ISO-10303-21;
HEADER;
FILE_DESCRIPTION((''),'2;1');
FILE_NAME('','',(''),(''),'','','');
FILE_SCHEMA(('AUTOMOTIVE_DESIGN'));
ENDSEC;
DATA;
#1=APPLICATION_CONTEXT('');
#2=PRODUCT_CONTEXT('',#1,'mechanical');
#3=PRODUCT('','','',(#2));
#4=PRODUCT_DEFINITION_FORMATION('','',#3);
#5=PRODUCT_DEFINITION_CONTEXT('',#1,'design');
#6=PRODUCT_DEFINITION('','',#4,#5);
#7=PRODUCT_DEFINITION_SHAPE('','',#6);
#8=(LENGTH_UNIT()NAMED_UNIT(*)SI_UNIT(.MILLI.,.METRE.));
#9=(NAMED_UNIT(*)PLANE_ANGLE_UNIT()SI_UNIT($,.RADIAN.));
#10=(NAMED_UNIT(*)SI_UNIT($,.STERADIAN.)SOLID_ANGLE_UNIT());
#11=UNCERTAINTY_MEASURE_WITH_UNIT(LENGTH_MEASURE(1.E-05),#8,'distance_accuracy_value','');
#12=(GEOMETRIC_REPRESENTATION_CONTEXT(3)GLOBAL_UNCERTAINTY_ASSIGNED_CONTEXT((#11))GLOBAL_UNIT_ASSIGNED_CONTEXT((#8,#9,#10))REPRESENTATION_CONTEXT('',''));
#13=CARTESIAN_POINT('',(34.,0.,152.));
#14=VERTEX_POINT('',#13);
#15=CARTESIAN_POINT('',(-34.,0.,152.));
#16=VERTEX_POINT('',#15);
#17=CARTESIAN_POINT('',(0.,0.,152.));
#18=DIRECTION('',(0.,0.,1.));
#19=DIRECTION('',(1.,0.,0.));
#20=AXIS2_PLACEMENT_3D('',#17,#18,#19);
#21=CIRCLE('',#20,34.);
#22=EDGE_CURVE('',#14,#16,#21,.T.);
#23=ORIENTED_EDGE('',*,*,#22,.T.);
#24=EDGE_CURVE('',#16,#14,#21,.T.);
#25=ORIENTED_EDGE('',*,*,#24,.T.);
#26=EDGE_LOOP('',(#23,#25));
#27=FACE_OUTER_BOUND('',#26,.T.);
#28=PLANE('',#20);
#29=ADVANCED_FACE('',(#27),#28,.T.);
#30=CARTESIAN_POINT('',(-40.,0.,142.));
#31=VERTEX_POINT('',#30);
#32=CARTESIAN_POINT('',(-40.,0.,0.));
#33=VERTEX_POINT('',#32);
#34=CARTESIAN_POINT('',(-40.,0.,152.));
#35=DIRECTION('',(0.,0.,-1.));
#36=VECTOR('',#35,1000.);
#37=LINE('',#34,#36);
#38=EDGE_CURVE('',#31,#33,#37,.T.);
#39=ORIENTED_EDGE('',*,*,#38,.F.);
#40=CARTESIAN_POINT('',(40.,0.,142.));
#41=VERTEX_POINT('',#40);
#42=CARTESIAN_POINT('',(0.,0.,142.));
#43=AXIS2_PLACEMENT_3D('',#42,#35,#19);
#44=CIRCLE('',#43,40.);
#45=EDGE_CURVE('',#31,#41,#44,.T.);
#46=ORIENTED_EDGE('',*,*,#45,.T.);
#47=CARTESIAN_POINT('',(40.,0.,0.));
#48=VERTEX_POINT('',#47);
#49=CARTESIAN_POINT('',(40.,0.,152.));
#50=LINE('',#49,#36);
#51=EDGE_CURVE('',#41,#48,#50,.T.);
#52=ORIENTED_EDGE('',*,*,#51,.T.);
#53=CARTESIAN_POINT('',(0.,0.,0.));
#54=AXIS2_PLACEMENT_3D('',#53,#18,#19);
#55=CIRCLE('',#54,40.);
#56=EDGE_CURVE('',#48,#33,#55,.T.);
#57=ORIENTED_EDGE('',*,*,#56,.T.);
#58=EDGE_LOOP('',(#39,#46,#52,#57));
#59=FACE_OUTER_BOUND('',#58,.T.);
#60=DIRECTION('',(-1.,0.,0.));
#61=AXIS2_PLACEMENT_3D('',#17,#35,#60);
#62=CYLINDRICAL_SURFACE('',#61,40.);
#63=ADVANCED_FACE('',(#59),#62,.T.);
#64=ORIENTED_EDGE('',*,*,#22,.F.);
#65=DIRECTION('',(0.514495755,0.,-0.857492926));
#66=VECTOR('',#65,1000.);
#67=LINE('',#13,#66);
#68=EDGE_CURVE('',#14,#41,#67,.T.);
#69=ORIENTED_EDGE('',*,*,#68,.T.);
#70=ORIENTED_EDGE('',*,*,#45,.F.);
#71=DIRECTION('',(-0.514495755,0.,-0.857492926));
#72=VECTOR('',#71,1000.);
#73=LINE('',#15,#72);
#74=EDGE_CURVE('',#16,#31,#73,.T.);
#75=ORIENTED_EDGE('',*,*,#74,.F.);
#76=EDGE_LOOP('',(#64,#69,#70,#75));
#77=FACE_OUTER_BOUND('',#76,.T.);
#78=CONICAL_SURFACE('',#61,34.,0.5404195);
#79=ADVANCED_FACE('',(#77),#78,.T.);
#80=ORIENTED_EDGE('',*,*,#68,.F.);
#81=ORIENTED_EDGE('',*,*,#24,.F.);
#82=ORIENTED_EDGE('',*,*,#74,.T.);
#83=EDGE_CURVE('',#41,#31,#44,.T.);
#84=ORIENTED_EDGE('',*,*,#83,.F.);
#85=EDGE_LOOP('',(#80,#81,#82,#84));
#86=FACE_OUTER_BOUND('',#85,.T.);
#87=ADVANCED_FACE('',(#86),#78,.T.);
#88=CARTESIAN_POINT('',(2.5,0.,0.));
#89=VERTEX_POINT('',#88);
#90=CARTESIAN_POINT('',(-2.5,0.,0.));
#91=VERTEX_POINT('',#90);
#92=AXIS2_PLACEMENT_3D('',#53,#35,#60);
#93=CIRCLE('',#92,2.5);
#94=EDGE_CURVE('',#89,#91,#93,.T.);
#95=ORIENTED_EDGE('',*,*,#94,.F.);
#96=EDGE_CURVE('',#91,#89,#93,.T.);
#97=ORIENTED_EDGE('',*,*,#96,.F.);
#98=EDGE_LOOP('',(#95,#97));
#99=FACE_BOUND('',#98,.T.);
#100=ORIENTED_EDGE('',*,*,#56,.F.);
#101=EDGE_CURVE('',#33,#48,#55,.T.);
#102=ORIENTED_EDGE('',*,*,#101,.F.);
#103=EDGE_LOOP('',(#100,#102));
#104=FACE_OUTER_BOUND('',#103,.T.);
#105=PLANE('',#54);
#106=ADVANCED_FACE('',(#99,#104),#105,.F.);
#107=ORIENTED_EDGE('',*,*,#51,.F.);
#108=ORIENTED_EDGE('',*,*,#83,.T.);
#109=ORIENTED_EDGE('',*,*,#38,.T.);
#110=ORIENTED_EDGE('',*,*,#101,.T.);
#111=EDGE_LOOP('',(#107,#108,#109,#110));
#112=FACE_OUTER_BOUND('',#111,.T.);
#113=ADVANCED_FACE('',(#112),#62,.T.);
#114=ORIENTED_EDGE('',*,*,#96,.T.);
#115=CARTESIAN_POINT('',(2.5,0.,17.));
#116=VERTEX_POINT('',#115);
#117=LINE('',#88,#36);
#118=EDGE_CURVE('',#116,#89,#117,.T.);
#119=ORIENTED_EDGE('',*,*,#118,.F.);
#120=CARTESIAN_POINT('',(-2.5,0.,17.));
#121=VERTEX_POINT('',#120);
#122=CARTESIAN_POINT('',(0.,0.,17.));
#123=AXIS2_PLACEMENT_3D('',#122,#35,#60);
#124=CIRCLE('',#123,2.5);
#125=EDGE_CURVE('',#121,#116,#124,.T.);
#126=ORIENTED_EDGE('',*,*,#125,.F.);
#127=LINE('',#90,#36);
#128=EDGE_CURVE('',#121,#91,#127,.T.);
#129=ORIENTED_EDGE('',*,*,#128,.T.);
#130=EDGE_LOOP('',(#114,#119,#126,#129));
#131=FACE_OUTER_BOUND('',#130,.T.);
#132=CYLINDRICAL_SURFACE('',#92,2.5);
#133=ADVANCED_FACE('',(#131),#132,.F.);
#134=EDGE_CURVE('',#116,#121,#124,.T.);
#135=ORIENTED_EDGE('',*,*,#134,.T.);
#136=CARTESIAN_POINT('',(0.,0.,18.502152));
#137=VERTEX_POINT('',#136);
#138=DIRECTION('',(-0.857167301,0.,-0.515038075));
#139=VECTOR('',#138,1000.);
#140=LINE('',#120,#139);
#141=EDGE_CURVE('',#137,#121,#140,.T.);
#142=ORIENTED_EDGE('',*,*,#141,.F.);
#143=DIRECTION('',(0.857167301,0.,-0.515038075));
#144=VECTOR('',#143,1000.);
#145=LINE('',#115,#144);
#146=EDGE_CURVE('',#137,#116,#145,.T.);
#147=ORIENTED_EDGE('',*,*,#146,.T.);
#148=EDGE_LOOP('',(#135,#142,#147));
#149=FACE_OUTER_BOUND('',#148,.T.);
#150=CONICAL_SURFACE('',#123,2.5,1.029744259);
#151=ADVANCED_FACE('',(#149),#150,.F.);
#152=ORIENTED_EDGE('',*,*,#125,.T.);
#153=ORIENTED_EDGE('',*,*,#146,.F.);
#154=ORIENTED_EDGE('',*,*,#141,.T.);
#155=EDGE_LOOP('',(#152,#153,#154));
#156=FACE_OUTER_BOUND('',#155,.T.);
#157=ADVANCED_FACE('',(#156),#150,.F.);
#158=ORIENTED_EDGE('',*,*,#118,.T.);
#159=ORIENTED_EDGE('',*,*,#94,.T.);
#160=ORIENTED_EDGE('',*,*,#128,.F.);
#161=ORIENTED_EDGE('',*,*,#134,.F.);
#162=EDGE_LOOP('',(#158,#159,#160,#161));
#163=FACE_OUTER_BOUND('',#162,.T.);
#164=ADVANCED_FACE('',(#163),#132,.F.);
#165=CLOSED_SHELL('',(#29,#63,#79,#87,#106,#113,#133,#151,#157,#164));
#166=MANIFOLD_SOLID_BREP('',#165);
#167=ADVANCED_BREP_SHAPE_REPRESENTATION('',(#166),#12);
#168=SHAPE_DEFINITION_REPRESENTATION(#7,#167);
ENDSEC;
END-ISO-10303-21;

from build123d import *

# Parameters (mm, degrees)
SKETCH1_R             = 40
BOSS_EXTRUDE1_DEPTH   = 152
CHAMFER1_SIZE         = 10
CHAMFER1_SIZE2        = 6
M6_TAPPED_HOLE1_D     = 5
M6_TAPPED_HOLE1_DEPTH = 17
M6_TAPPED_HOLE1_TIP   = 1.502151548


with BuildPart() as part:
    # Sketch1 → Boss-Extrude1 (new body)
    with BuildSketch(Plane.XY):
        Circle(SKETCH1_R)
    extrude(amount=BOSS_EXTRUDE1_DEPTH)

    # Chamfer1
    chamfer1_edges = [part.edges().sort_by_distance(p)[0] for p in [
        (-40, 0, 152),
    ]]
    chamfer1_side = [part.faces().sort_by_distance(p)[0] for p in [
        (-40, 0, 76),
    ]]
    chamfer(chamfer1_edges, length=CHAMFER1_SIZE, length2=CHAMFER1_SIZE2, reference=chamfer1_side[0])

    # M6 Tapped Hole1
    with Locations(Plane(origin=(0, 0, 0), x_dir=(-1, 0, 0), z_dir=(0, 0, -1))):
        with Locations((0, 0)):
            Hole(M6_TAPPED_HOLE1_D / 2, depth=M6_TAPPED_HOLE1_DEPTH)
            with Locations((0, 0, -(M6_TAPPED_HOLE1_DEPTH + M6_TAPPED_HOLE1_TIP / 2))):  # 118° drill point
                Cone(0, M6_TAPPED_HOLE1_D / 2, M6_TAPPED_HOLE1_TIP, mode=Mode.SUBTRACT)


solid = part.part
